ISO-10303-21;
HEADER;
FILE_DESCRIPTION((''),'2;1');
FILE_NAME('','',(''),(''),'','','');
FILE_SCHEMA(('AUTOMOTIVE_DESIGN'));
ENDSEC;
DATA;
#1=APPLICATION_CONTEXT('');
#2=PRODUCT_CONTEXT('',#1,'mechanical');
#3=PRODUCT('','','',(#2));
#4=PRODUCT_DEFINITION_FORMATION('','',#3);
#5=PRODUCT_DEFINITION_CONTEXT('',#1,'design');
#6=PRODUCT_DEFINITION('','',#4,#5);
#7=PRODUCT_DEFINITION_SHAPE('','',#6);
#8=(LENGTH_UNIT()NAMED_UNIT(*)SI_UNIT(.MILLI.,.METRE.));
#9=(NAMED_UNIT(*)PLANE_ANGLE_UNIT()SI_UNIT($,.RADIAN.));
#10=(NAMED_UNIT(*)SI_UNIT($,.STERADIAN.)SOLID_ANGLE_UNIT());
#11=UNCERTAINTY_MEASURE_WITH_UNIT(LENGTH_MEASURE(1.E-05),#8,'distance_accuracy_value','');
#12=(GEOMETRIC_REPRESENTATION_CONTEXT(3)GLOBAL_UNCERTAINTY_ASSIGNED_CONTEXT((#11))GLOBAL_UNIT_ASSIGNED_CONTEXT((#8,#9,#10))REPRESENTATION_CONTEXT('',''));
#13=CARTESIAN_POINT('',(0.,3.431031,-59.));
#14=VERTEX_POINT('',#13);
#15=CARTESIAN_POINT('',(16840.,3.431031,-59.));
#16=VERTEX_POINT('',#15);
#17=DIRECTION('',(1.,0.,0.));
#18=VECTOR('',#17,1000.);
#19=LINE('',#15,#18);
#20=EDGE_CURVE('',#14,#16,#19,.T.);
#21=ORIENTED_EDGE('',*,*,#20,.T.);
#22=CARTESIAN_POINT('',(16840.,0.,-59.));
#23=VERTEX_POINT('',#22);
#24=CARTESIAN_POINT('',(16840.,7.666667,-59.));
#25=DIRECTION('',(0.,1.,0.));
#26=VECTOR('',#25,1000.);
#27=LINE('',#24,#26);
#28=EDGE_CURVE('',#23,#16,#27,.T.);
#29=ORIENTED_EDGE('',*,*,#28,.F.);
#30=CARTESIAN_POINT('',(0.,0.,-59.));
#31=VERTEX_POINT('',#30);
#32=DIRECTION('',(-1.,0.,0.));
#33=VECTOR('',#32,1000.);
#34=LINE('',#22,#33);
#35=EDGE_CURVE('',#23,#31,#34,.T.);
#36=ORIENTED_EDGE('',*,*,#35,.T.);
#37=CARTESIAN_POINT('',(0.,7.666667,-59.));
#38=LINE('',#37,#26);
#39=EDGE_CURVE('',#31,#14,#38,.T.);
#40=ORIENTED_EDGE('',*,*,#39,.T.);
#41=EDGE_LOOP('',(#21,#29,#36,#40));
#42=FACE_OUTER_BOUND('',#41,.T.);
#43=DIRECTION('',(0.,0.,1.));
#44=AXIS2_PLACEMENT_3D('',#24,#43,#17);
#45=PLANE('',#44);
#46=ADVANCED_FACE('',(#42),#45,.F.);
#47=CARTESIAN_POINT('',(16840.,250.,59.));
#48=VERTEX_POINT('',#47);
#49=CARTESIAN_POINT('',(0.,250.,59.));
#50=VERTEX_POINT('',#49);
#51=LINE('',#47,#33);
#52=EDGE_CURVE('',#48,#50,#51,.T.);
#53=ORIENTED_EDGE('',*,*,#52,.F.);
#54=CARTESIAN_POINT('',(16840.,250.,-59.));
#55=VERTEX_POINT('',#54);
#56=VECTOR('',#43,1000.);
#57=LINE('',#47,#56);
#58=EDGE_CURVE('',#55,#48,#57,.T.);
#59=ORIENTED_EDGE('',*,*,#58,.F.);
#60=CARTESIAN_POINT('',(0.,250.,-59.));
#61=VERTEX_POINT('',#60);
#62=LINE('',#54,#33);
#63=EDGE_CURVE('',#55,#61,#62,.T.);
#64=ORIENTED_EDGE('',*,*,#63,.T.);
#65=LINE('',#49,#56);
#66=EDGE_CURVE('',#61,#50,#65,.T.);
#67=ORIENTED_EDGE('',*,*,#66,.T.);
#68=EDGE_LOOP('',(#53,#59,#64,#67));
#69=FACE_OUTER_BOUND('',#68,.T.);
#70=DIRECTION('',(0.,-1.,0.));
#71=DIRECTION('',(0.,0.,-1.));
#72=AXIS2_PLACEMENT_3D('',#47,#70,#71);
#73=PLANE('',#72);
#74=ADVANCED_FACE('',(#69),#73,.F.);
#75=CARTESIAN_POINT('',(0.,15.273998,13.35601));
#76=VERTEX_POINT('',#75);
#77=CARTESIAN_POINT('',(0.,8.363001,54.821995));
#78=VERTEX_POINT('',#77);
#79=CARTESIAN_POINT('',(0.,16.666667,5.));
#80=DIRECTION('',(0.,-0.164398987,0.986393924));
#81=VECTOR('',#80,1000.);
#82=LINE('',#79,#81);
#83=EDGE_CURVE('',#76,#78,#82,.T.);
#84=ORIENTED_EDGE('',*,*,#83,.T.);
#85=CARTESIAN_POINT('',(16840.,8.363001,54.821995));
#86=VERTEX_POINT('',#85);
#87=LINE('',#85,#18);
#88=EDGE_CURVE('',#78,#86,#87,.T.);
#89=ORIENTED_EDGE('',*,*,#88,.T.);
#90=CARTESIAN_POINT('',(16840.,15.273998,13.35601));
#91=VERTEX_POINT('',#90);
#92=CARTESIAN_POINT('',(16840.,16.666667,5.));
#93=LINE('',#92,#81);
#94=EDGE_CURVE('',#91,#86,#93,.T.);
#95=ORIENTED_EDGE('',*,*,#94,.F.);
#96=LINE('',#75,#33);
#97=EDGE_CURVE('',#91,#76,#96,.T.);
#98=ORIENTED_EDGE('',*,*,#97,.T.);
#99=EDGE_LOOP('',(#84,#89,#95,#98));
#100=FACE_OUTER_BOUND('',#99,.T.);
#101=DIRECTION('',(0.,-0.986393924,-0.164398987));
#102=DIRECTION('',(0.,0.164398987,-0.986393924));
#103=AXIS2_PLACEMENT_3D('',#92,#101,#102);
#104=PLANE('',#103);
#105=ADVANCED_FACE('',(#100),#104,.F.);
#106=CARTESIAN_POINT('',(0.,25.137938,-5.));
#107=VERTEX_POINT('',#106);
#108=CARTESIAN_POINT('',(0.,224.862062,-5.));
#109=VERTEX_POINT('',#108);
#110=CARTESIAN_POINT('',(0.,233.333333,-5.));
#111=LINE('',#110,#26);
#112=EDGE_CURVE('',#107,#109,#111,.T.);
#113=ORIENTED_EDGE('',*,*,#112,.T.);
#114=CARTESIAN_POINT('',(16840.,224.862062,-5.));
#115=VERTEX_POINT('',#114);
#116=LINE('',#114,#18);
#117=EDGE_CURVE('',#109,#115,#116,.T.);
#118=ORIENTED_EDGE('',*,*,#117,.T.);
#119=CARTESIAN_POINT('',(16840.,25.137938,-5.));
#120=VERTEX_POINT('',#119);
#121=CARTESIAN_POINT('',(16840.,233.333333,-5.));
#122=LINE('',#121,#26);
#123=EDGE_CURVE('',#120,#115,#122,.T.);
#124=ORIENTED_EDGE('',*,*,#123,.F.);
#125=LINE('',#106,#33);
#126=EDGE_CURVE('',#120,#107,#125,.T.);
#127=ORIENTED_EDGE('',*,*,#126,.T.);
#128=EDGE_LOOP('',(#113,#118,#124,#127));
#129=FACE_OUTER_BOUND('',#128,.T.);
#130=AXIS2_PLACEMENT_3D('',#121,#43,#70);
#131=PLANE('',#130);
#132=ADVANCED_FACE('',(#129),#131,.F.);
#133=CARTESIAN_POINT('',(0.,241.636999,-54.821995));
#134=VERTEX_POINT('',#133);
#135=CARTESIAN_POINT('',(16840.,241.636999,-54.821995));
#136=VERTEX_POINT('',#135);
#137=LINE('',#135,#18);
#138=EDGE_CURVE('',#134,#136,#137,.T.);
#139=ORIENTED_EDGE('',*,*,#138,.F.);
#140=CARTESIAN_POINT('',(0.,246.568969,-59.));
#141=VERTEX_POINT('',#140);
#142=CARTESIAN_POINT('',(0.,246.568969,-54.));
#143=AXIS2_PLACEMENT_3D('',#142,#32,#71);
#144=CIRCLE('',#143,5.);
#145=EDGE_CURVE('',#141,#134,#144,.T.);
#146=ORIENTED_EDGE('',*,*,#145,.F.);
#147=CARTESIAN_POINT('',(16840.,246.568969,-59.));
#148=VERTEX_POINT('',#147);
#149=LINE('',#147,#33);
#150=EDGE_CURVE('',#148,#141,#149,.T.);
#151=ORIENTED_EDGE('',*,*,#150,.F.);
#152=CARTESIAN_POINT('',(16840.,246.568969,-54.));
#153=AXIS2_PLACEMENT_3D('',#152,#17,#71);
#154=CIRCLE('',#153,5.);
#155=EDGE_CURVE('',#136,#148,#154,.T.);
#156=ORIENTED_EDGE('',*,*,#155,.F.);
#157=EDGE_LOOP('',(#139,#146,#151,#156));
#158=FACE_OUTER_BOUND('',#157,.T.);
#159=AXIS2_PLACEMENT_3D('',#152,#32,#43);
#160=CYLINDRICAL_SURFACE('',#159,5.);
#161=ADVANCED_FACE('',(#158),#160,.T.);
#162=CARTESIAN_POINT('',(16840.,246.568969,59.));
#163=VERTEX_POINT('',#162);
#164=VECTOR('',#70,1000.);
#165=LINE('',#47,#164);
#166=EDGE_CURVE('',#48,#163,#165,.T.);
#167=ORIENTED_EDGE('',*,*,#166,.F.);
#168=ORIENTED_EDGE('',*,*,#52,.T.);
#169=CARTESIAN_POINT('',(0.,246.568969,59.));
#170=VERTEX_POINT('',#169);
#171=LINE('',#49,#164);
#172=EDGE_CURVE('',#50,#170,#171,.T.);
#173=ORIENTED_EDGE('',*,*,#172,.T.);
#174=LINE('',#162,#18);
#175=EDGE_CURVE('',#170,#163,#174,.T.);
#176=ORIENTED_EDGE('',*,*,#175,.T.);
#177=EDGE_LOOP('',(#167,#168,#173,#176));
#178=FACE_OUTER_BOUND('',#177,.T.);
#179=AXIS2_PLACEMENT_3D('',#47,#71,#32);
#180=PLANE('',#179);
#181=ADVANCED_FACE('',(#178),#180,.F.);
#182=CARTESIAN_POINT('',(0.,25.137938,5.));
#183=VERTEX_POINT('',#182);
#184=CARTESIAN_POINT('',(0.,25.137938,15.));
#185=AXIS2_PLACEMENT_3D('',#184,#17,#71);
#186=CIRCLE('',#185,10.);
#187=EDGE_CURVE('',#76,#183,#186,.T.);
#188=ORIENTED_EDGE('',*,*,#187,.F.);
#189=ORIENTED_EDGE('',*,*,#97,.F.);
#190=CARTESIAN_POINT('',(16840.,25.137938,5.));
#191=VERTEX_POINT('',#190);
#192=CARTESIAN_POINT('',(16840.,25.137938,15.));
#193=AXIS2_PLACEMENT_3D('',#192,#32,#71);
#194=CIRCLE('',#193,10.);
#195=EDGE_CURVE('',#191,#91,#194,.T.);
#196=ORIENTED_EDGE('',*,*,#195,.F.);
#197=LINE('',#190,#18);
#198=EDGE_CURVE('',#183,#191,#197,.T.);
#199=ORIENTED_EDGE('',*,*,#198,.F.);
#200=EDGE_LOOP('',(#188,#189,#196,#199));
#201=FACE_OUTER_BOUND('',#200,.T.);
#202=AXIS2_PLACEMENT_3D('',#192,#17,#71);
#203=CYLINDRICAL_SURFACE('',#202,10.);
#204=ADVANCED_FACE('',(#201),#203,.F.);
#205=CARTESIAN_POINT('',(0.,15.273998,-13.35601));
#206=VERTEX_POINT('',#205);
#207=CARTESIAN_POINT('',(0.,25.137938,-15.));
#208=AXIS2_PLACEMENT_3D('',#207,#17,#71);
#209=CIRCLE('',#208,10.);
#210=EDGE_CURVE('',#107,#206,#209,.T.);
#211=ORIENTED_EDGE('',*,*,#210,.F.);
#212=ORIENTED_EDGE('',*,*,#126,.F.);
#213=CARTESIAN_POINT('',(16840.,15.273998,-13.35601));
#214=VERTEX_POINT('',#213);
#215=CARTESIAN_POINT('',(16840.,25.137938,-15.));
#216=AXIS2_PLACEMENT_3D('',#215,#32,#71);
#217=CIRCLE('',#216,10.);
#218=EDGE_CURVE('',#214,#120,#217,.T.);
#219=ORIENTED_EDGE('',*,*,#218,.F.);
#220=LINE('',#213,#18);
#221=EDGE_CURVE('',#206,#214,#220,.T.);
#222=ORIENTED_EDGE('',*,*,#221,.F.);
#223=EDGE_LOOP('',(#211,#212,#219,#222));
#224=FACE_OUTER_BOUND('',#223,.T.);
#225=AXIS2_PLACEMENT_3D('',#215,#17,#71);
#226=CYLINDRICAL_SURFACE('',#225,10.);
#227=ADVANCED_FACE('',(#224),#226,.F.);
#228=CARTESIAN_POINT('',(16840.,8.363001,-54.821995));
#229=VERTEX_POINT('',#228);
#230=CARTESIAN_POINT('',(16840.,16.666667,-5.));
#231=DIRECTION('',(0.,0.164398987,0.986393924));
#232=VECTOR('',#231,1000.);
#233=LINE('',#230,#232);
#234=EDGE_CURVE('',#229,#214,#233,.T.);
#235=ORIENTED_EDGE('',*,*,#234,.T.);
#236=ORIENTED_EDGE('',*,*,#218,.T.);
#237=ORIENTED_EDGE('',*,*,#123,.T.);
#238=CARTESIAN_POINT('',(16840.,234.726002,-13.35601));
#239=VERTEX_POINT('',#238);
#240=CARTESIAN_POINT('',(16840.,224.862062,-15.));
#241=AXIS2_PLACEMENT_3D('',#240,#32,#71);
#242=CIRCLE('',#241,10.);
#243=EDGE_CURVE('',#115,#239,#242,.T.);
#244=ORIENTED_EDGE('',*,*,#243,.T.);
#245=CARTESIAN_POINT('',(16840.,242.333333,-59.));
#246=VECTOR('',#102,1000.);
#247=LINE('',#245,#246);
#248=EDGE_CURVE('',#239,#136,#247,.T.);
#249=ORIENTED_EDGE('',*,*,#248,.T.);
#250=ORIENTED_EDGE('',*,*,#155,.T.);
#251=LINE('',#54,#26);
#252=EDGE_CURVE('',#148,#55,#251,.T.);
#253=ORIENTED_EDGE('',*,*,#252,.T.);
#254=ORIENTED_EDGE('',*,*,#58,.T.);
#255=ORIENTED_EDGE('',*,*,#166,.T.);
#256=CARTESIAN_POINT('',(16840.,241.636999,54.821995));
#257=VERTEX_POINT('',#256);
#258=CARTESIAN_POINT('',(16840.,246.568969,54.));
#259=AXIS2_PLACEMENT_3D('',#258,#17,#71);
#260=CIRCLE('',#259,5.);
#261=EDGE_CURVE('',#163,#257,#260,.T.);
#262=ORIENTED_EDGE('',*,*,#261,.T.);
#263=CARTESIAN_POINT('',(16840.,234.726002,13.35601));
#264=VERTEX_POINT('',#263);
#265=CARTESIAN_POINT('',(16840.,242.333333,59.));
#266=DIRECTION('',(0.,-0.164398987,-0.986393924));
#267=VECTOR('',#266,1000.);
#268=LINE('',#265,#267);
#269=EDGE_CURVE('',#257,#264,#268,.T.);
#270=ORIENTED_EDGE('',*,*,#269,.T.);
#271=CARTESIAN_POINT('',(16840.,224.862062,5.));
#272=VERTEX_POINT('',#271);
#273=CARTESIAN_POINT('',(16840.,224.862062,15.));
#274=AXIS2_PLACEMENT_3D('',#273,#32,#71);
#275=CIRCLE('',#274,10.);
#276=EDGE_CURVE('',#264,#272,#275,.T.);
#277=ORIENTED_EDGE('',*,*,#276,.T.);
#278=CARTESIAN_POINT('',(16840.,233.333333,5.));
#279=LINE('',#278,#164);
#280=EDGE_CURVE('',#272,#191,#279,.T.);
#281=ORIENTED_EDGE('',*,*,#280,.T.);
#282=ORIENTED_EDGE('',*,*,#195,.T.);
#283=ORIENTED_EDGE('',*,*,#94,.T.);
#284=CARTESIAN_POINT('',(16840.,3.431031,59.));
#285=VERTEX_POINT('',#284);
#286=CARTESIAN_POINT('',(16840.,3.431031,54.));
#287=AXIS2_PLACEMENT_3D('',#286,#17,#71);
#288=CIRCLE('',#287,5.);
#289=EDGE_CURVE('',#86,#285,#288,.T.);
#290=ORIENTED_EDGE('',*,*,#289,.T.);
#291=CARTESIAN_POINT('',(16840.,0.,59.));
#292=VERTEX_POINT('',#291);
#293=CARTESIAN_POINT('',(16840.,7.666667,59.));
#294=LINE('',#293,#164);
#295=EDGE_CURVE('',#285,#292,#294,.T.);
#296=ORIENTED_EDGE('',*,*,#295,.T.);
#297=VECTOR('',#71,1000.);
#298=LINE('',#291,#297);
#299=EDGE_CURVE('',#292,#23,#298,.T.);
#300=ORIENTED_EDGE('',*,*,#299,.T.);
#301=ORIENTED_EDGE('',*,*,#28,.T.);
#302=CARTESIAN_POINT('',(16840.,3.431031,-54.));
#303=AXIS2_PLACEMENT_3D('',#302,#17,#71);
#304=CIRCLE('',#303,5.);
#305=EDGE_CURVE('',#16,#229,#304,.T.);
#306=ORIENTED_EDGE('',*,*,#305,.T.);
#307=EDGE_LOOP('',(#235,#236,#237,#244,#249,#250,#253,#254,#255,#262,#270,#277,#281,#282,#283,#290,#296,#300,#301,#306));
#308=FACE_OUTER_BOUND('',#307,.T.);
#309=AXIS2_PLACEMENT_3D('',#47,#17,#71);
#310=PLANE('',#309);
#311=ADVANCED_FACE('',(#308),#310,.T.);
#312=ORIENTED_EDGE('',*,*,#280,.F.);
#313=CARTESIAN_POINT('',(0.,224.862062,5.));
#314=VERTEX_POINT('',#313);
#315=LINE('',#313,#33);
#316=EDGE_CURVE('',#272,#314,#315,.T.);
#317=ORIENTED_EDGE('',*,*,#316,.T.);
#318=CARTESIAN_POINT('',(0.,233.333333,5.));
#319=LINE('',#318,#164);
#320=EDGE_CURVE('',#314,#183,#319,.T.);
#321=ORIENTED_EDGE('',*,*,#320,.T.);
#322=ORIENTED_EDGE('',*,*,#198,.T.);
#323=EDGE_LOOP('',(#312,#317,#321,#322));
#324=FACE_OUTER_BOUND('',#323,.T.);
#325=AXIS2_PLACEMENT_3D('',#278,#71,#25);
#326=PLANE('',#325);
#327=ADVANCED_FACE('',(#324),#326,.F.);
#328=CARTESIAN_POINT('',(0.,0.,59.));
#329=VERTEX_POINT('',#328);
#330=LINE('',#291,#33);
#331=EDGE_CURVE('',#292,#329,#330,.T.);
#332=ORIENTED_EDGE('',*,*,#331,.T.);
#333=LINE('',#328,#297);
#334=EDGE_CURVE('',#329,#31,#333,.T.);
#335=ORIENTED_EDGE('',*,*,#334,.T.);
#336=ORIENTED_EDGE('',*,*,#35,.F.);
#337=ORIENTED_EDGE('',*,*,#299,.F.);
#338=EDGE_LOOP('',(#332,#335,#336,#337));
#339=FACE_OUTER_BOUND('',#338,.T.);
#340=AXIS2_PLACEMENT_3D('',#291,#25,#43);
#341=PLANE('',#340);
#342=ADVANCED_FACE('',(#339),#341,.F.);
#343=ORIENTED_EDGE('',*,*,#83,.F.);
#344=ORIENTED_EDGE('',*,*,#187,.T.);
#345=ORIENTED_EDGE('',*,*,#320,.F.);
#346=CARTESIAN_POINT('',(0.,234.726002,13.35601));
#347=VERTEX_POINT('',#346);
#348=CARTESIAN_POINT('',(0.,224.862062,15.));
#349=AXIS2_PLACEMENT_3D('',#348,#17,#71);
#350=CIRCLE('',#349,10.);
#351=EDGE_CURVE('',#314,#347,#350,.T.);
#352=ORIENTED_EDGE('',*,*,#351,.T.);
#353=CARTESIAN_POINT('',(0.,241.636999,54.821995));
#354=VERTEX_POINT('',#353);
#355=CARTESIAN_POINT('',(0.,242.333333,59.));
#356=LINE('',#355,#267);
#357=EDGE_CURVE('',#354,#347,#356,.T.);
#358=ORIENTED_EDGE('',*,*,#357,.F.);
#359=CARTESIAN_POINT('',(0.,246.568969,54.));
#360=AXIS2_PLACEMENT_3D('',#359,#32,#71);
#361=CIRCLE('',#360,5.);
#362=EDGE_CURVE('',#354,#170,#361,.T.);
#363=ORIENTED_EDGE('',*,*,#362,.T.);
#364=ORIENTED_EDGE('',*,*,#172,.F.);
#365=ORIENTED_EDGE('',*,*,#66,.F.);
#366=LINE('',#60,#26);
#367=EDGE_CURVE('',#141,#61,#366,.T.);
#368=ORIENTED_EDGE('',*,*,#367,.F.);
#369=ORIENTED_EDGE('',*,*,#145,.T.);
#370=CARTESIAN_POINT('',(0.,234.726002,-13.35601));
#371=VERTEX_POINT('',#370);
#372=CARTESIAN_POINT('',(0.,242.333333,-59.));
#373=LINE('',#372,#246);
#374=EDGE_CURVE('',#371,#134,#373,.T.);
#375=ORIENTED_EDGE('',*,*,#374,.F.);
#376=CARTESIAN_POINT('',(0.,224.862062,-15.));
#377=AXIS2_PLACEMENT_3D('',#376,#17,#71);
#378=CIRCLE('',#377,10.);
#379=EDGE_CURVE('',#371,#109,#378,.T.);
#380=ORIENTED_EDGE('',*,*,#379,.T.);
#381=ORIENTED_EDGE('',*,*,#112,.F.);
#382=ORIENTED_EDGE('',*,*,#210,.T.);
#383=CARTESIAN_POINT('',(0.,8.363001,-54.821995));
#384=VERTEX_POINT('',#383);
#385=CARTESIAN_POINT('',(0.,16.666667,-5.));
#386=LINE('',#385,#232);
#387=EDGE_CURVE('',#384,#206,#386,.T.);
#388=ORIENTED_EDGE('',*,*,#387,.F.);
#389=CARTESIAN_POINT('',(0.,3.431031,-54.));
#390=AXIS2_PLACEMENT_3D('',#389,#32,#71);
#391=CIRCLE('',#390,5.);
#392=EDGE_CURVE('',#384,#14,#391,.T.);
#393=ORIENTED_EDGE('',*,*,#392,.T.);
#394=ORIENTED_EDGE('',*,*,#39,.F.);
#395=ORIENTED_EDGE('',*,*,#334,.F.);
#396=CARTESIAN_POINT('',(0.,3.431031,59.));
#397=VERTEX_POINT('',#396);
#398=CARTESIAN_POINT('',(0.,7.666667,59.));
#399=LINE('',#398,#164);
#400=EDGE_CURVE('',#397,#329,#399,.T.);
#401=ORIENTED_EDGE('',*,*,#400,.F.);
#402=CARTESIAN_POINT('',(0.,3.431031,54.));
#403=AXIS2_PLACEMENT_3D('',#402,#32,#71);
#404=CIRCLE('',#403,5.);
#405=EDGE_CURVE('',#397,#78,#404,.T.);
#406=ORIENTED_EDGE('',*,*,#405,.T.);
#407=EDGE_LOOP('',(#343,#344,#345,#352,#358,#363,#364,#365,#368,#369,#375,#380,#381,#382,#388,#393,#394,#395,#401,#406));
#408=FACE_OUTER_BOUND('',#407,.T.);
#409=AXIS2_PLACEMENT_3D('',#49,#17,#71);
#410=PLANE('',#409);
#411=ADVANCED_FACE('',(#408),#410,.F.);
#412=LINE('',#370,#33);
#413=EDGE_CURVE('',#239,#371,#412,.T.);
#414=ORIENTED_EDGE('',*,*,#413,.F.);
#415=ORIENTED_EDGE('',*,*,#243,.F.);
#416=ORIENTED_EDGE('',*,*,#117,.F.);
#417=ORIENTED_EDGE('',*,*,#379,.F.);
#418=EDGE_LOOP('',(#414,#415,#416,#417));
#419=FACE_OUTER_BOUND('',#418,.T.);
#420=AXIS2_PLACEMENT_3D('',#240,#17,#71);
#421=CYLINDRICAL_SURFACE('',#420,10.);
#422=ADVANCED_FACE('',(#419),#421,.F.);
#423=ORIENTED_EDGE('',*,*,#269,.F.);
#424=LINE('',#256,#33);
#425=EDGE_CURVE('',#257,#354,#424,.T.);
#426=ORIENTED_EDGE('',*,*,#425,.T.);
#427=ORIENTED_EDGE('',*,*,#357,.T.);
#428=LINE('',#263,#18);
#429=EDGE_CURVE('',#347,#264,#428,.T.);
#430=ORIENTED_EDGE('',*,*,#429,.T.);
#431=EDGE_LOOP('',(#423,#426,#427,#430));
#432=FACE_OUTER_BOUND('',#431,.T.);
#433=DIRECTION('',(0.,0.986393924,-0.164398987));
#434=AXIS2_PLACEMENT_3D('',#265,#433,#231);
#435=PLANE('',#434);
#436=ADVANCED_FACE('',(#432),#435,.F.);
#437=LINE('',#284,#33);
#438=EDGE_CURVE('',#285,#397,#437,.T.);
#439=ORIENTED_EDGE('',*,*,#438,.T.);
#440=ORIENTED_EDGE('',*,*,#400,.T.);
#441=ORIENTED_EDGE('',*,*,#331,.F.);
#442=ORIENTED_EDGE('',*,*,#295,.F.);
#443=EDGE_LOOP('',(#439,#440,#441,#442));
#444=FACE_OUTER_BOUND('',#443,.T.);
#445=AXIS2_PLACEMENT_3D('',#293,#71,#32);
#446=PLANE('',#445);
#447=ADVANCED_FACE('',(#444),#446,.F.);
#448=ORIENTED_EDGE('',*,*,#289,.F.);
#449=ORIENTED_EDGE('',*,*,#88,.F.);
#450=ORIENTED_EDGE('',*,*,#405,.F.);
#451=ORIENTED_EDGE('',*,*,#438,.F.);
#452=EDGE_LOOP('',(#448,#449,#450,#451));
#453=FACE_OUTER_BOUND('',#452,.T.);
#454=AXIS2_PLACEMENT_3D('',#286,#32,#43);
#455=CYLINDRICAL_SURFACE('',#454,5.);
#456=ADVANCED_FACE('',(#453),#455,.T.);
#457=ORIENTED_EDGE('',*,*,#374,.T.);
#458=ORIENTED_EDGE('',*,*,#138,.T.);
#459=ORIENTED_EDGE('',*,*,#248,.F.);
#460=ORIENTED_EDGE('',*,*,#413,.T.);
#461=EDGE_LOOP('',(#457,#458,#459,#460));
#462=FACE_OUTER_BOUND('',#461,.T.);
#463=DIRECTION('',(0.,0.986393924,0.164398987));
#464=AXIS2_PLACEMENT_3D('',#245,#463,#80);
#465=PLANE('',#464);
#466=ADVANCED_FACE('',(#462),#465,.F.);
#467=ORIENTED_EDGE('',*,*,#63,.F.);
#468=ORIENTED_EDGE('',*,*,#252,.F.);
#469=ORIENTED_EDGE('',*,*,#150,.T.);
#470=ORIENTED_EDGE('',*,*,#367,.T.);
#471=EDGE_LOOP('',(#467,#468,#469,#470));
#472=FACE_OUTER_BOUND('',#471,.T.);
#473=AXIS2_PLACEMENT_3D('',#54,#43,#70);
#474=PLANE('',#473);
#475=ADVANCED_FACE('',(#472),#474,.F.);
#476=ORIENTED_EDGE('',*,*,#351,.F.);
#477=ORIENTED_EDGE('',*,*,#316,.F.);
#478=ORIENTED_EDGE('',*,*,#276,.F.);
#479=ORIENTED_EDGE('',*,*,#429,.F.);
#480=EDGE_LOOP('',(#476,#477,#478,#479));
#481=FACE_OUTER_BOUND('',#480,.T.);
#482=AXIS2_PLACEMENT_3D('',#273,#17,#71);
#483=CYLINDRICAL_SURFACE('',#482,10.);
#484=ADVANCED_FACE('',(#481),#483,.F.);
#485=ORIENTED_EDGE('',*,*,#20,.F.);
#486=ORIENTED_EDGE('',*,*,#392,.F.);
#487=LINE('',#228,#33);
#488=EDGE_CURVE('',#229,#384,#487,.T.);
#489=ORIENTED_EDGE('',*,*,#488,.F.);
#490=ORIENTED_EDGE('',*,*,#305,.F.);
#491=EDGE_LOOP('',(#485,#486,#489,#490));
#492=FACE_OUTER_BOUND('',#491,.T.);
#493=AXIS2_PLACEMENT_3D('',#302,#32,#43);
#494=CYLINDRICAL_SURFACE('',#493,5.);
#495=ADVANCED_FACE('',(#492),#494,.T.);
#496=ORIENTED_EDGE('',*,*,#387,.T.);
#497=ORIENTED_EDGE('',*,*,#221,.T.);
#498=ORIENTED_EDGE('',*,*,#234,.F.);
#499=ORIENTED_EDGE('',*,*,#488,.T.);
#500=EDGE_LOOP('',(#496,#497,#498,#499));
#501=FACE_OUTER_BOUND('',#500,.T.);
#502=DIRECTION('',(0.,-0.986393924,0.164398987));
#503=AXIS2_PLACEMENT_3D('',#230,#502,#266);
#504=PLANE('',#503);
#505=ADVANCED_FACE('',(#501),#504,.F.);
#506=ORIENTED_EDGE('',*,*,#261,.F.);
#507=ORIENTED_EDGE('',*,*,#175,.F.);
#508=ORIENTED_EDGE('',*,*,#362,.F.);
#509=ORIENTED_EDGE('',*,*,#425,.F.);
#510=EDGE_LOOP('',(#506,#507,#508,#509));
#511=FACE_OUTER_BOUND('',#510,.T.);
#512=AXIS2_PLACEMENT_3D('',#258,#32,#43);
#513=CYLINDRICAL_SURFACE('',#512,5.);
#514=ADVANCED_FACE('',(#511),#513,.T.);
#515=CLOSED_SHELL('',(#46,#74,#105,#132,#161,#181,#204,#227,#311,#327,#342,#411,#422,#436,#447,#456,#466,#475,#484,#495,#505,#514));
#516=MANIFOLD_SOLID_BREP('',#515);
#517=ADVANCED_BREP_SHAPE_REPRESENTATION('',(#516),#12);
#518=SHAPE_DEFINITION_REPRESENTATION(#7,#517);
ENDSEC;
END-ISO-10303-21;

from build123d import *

# Parameters (mm, degrees)
BASE_DEPTH = 16840
FILLET1_R  = 10
FILLET2_R  = 5


with BuildPart() as part:
    # Sketch1 → Base (new body)
    with BuildSketch(Plane(origin=(0, 0, 0), x_dir=(0, 0, -1), z_dir=(1, 0, 0))):
        Polygon((-59, 0), (59, 0), (59, 7.666666667), (5, 16.666666667), (5, 233.333333333), (59, 242.333333333), (59, 250), (-59, 250), (-59, 242.333333333), (-5, 233.333333333), (-5, 16.666666667), (-59, 7.666666667), align=None)
    extrude(amount=BASE_DEPTH)

    # Fillet1
    fillet1_edges = [part.edges().sort_by_distance(p)[0] for p in [
        (8420, 16.666666667, 5),
        (8420, 233.333333333, 5),
        (8420, 233.333333333, -5),
        (8420, 16.666666667, -5),
    ]]
    fillet(fillet1_edges, radius=FILLET1_R)

    # Fillet2
    fillet2_edges = [part.edges().sort_by_distance(p)[0] for p in [
        (8420, 7.666666667, 59),
        (8420, 242.333333333, 59),
        (8420, 242.333333333, -59),
        (8420, 7.666666667, -59),
    ]]
    fillet(fillet2_edges, radius=FILLET2_R)


solid = part.part
